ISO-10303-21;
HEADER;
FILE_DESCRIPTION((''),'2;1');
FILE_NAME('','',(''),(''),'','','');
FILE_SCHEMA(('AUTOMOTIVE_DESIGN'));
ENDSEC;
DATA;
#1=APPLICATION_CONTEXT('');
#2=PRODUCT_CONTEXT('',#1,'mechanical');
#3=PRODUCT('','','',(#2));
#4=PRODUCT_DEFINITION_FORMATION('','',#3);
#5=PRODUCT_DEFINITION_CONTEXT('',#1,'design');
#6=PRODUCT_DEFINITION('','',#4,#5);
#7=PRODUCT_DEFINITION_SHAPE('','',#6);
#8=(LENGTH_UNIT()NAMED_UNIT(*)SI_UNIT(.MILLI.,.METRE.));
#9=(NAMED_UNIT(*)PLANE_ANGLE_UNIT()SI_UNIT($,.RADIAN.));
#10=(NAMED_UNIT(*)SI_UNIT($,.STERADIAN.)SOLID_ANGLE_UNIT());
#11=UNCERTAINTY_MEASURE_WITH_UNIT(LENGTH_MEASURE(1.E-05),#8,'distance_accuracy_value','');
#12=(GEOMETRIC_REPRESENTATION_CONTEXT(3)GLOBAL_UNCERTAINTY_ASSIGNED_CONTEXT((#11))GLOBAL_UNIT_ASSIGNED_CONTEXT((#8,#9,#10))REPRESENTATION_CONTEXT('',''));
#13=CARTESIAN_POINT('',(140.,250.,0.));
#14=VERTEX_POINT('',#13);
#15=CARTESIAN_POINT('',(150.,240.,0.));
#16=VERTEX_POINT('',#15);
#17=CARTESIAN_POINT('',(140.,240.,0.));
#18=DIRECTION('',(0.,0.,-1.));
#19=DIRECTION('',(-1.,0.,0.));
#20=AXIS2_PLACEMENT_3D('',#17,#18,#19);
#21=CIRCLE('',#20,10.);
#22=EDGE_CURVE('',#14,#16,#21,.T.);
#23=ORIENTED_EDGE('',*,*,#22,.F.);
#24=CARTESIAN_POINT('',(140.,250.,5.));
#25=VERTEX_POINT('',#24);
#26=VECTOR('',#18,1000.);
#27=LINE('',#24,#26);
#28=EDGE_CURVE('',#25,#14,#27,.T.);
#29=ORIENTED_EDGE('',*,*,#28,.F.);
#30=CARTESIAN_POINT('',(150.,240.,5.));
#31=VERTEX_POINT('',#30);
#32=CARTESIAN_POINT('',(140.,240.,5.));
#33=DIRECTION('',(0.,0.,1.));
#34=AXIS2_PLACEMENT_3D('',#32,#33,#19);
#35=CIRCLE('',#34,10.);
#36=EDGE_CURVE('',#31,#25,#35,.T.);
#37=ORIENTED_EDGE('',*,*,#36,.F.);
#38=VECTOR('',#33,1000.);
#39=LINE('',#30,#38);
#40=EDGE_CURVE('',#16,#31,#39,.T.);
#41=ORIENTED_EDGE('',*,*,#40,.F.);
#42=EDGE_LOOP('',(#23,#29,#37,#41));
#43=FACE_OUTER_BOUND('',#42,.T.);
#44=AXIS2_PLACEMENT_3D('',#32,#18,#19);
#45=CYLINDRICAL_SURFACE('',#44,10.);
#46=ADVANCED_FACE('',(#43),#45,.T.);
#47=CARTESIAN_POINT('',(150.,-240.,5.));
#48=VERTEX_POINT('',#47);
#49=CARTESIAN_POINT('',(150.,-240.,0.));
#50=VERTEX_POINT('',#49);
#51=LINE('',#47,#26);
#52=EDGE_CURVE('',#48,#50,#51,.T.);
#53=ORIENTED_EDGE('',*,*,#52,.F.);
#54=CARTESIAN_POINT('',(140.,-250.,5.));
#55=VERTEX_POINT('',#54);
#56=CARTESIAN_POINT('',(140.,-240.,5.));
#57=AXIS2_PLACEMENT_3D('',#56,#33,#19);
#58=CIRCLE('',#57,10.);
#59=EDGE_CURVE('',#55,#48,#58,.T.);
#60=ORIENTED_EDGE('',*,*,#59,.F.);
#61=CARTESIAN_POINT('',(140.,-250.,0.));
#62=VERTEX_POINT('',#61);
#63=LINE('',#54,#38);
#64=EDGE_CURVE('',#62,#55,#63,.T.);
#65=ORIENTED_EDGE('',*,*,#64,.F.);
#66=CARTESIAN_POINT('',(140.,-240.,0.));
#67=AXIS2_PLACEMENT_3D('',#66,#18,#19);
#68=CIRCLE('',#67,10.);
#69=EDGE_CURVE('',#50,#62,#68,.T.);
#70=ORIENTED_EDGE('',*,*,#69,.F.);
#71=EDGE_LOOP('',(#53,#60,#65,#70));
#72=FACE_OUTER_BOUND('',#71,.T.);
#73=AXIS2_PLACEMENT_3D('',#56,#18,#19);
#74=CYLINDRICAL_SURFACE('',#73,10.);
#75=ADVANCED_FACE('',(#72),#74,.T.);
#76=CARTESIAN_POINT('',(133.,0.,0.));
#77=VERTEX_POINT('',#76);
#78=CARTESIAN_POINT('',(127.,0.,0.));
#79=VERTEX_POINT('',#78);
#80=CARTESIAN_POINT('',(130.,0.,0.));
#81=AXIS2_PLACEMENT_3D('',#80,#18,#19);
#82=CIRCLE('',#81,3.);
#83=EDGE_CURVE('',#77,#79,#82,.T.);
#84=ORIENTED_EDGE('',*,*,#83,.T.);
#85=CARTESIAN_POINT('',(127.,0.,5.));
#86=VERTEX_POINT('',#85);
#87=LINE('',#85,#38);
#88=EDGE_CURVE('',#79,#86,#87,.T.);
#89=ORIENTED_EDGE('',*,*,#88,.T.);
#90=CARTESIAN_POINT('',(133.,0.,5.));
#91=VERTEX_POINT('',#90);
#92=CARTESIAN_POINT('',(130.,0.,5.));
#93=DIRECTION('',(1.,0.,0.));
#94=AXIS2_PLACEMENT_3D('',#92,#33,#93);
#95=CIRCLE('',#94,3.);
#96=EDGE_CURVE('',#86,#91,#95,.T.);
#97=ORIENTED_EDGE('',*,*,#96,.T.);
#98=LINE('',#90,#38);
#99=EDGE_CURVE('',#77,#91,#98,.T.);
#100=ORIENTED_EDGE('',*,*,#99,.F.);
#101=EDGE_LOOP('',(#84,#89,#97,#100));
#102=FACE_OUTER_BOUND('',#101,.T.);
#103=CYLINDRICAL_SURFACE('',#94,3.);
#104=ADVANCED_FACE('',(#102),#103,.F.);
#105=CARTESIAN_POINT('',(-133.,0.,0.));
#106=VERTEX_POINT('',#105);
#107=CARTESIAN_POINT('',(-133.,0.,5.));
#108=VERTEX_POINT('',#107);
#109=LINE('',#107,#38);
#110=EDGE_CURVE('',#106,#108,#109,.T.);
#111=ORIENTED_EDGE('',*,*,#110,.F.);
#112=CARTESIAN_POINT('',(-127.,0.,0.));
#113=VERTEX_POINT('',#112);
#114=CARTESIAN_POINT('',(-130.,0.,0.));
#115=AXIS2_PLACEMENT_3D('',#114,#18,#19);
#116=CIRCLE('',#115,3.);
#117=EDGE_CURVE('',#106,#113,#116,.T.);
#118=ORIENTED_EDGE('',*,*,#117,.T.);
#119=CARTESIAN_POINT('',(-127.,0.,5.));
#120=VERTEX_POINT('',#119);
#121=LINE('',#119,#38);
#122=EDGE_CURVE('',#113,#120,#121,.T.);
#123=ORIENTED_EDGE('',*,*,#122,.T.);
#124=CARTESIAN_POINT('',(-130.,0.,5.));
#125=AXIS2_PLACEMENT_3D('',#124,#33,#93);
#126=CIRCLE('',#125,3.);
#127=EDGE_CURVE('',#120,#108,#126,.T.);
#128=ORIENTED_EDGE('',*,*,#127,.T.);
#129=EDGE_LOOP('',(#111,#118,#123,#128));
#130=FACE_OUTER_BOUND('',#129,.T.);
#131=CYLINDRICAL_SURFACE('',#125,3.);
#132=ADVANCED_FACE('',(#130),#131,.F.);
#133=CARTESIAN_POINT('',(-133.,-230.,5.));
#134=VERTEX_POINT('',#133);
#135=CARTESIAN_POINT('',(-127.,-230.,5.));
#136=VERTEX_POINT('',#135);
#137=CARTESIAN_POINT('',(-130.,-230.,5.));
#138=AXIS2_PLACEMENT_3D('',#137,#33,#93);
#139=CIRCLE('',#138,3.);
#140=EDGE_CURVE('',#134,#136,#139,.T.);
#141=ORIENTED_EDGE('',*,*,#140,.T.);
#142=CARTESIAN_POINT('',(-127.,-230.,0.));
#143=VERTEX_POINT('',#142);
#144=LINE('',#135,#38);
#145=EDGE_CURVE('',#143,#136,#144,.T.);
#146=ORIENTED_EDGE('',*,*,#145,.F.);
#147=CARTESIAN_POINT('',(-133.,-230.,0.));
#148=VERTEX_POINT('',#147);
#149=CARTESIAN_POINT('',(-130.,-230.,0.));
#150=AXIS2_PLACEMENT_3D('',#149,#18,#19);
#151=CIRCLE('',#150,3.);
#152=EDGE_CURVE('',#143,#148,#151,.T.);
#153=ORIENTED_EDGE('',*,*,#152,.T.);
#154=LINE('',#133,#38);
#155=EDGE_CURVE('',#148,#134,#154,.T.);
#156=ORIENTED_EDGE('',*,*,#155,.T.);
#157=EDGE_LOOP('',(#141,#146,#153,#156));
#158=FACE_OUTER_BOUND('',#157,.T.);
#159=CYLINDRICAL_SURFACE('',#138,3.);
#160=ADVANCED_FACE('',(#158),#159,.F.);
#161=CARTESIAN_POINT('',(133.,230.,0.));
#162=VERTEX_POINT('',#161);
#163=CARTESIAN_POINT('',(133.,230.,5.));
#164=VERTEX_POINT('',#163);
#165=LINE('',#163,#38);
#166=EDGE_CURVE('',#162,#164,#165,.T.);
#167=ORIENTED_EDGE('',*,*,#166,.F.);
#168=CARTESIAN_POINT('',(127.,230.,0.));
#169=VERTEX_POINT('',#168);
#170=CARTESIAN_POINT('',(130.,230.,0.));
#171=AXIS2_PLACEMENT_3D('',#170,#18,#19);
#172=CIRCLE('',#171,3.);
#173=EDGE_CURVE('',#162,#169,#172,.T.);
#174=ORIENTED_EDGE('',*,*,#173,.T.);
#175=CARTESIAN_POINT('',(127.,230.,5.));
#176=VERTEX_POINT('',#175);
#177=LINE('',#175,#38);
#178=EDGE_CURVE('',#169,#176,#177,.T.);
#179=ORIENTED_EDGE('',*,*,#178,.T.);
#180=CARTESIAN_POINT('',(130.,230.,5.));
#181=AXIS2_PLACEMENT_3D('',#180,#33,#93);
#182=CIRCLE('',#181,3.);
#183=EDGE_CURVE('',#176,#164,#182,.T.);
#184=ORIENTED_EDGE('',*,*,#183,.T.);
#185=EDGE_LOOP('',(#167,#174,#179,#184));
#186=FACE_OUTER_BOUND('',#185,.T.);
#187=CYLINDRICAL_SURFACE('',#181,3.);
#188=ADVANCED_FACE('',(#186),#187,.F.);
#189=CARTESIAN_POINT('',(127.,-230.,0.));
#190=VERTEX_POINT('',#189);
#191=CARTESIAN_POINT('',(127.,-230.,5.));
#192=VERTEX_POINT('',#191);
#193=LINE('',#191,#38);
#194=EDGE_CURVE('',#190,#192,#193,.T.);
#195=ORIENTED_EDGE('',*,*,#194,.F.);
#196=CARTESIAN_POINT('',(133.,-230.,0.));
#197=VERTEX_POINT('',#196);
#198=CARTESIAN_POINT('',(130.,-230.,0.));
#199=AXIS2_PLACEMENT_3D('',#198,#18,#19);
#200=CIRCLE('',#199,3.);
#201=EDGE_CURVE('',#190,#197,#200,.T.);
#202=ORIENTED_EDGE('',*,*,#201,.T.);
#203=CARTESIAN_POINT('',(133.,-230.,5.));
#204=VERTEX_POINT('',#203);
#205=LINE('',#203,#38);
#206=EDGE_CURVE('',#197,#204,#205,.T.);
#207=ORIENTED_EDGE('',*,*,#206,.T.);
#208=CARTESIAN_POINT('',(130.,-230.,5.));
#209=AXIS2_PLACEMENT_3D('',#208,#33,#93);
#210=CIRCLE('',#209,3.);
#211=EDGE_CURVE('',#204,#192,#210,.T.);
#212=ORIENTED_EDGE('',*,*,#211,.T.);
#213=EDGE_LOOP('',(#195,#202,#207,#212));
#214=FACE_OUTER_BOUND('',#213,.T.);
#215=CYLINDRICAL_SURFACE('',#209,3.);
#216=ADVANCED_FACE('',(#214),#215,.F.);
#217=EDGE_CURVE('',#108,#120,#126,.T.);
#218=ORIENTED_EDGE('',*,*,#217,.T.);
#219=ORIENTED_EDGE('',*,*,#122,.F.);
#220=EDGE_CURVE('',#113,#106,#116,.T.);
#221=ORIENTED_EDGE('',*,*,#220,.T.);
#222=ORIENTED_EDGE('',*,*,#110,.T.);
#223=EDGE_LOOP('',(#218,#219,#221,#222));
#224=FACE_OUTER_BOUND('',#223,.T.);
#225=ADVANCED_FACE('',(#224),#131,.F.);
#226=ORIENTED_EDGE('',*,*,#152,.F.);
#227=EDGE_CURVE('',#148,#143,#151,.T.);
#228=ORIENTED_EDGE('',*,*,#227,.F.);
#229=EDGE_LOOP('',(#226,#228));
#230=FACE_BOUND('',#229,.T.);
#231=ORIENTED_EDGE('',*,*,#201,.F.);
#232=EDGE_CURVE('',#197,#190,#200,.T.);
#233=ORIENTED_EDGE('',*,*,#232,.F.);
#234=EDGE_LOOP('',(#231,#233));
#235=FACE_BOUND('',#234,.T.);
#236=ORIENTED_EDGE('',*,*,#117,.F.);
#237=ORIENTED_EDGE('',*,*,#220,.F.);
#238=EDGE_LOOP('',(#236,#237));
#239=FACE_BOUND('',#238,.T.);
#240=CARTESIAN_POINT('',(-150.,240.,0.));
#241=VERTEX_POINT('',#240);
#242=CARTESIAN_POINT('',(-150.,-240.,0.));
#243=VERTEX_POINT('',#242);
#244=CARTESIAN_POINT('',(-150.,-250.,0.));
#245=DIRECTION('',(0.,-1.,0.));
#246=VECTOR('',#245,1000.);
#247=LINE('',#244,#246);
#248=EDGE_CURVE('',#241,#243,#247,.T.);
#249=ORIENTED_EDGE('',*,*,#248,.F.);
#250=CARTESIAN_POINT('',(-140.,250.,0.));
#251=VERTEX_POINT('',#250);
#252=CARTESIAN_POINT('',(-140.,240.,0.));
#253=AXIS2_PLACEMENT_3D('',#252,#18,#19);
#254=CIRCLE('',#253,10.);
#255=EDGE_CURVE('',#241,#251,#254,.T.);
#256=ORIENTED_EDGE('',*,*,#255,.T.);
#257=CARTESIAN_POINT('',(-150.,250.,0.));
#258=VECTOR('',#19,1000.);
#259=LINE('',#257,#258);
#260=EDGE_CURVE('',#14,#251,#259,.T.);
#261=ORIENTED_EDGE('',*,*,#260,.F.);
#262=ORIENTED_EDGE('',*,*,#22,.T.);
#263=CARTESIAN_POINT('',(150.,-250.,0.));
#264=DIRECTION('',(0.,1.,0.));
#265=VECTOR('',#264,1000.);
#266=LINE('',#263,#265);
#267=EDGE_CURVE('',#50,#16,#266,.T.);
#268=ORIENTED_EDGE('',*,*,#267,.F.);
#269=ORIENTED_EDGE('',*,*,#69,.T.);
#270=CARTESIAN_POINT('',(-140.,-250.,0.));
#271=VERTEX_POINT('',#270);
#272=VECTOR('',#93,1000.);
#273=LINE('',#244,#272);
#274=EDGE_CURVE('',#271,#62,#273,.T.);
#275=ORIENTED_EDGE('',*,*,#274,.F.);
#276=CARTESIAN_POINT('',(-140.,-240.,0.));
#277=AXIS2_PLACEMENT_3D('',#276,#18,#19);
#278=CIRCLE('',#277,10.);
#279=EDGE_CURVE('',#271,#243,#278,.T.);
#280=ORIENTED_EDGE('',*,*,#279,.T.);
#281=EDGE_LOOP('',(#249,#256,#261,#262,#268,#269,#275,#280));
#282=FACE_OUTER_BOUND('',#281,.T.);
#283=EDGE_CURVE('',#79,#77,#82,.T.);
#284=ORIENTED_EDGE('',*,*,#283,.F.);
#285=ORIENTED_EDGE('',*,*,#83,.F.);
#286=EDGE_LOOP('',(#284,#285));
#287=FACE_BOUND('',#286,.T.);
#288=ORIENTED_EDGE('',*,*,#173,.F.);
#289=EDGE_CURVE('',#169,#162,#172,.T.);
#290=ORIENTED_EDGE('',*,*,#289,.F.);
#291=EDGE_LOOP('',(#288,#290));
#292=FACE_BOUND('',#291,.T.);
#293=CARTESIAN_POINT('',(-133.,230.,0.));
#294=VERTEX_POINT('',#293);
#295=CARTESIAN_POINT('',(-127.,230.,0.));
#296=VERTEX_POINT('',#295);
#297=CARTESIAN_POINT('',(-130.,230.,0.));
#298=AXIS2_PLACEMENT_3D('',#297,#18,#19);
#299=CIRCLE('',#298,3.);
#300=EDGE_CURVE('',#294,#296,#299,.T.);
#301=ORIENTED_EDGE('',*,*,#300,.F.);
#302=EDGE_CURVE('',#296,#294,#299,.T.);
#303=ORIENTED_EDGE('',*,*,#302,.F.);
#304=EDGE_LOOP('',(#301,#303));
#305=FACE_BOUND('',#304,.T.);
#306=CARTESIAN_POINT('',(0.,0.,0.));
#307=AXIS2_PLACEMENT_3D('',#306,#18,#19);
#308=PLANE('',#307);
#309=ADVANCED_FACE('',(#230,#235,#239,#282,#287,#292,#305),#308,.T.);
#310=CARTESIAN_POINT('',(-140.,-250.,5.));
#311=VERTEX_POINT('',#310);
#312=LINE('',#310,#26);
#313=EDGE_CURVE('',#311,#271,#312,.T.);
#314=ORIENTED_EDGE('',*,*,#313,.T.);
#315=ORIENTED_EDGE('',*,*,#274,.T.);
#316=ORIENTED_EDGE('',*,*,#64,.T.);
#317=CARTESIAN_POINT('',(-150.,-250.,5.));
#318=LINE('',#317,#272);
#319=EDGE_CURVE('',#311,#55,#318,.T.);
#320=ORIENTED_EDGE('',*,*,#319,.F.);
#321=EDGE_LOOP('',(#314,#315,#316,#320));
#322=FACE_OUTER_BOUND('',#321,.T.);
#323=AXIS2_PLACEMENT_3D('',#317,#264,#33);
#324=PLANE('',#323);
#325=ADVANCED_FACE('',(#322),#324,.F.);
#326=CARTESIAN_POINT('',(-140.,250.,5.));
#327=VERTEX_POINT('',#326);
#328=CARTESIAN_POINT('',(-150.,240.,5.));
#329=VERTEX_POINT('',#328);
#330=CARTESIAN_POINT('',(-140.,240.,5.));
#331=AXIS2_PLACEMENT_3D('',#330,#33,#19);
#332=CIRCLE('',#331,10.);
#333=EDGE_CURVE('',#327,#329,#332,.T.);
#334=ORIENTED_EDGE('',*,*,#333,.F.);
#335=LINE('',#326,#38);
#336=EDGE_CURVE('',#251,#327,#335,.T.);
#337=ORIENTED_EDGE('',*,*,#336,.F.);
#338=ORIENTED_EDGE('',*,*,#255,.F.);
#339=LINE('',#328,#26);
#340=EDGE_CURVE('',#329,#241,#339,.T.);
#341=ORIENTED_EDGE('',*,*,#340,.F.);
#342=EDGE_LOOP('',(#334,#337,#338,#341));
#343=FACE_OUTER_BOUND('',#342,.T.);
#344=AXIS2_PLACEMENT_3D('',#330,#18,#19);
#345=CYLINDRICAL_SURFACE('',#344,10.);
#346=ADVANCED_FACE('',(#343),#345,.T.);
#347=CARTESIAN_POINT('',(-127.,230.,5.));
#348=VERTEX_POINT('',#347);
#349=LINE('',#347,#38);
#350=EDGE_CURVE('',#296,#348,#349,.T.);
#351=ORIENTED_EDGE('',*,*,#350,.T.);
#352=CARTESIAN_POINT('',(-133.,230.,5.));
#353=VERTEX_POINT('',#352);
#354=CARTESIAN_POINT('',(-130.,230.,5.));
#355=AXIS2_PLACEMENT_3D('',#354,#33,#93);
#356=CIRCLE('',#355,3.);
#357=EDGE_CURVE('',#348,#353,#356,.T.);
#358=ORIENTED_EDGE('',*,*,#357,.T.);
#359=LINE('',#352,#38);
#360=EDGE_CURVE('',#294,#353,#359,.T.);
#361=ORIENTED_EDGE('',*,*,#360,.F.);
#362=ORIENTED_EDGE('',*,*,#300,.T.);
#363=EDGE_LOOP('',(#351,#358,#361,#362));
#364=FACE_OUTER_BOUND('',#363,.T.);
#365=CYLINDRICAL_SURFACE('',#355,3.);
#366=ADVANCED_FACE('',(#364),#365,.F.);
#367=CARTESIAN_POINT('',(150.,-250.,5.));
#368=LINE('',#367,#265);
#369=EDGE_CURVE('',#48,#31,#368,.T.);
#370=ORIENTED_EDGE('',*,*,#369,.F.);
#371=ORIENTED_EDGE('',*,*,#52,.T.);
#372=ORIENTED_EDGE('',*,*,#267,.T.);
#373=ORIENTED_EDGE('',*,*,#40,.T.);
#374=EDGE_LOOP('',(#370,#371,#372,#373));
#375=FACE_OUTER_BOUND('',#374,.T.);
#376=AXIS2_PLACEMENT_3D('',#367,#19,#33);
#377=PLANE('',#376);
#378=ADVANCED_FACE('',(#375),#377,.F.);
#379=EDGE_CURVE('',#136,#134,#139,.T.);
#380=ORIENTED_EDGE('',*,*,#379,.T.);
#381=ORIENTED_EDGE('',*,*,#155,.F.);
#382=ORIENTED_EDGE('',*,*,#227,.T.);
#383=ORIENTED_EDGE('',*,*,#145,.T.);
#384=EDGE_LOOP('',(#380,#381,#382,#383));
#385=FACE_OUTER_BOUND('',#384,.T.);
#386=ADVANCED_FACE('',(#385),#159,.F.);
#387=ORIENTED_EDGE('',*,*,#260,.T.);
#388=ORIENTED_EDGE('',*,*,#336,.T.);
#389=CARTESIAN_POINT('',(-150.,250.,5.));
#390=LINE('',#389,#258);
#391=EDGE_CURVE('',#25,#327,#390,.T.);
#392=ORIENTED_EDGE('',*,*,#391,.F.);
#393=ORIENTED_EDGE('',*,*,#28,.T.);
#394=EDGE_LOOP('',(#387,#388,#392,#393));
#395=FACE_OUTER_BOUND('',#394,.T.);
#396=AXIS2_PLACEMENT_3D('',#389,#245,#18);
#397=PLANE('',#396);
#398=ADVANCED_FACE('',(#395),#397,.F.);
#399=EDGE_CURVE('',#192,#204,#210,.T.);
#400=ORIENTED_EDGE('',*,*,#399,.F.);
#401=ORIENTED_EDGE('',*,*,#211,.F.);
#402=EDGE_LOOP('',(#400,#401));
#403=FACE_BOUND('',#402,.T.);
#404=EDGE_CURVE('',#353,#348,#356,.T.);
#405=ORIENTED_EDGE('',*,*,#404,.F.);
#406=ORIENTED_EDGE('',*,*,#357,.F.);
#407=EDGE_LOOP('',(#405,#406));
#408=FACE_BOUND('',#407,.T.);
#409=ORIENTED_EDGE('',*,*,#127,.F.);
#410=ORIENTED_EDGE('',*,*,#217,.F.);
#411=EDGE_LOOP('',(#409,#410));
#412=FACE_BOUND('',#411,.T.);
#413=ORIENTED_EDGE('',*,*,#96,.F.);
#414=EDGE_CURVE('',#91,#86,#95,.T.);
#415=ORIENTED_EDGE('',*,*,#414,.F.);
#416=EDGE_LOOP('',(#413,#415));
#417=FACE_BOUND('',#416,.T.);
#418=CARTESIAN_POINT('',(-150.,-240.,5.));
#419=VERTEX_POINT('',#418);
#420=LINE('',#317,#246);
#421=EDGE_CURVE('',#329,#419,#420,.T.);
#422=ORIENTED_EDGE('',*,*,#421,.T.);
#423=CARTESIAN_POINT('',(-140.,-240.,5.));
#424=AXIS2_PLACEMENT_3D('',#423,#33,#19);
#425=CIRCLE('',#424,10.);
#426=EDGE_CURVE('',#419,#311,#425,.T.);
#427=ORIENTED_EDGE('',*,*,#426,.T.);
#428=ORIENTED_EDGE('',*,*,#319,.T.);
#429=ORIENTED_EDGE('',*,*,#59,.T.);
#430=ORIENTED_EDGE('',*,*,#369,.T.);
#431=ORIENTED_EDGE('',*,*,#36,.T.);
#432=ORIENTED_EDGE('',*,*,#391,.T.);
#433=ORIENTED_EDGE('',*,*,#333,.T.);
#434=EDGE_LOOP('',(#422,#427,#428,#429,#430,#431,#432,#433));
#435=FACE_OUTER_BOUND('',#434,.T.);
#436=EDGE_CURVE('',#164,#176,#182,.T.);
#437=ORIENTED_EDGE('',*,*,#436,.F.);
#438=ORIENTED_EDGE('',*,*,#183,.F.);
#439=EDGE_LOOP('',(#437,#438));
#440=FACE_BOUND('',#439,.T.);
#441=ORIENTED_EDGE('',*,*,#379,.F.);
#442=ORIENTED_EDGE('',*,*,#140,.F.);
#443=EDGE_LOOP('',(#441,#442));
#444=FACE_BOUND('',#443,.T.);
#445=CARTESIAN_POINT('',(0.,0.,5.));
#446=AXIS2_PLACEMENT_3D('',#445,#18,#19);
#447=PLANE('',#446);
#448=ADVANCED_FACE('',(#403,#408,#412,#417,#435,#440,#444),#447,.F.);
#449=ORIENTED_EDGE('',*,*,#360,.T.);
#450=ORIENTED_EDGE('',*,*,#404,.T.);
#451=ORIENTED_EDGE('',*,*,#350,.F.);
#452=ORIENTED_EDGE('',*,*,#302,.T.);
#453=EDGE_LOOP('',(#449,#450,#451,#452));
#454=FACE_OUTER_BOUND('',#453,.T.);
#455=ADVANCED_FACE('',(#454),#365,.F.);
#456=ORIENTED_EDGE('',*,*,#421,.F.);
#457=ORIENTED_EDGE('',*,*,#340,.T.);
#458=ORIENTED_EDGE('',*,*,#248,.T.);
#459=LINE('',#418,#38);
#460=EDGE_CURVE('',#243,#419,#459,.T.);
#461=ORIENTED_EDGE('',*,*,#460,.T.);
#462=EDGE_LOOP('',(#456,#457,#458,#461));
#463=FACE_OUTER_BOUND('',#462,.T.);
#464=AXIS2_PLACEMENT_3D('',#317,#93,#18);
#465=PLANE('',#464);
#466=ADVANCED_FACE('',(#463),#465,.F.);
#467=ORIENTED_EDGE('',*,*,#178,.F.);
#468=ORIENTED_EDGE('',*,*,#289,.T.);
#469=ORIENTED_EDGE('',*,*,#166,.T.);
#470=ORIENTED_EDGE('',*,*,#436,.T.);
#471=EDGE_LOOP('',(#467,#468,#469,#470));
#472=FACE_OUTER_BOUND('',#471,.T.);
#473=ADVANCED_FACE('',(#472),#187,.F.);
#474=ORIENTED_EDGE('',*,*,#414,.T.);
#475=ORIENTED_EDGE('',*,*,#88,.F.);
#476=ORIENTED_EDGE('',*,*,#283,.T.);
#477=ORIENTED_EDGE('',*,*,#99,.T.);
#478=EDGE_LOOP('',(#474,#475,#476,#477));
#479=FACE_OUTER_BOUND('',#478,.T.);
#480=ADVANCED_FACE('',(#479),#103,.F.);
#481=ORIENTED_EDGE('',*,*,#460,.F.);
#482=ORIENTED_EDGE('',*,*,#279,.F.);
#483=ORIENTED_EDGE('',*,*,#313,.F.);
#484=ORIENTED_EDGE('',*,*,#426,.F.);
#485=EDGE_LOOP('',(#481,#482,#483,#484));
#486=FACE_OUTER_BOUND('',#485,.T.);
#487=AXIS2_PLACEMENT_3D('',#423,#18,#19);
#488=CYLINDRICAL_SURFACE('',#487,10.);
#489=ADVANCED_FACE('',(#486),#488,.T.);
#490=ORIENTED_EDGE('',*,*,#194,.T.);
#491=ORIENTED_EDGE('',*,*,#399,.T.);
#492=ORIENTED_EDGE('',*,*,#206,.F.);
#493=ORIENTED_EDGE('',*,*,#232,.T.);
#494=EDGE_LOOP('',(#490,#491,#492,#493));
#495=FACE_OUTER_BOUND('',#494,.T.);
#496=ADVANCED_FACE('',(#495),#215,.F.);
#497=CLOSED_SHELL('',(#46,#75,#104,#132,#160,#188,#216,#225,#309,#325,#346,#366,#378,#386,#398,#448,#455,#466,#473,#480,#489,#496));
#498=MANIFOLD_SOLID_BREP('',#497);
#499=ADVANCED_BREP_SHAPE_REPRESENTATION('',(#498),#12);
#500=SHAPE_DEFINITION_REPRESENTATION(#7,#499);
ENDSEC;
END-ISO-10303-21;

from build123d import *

# Parameters (mm, degrees)
SKETCH_1_W                = 300
SKETCH_1_H                = 500
EXTRUDE_1_DEPTH           = 5
HOLE_WIZARD_6_0_6_1_D     = 6
HOLE_WIZARD_6_0_6_1_DEPTH = 27.75
HOLE_WIZARD_6_0_6_1_TIP   = 1.802581857
FILLET_1_R                = 10


with BuildPart() as part:
    # 草图1 → 凸台-拉伸1 (new body)
    with BuildSketch(Plane.XY):
        Rectangle(SKETCH_1_W, SKETCH_1_H)
    extrude(amount=EXTRUDE_1_DEPTH)

    # Ø6.0 (6) 直径孔1
    with Locations(Plane.XY.offset(5)):
        with Locations((-130, 230), (130, 230), (130, -230), (-130, -230), (-130, 0), (130, 0)):
            Hole(HOLE_WIZARD_6_0_6_1_D / 2, depth=HOLE_WIZARD_6_0_6_1_DEPTH)
            with Locations((0, 0, -(HOLE_WIZARD_6_0_6_1_DEPTH + HOLE_WIZARD_6_0_6_1_TIP / 2))):  # 118° drill point
                Cone(0, HOLE_WIZARD_6_0_6_1_D / 2, HOLE_WIZARD_6_0_6_1_TIP, mode=Mode.SUBTRACT)

    # 圆角1
    fillet_1_edges = [part.edges().sort_by_distance(p)[0] for p in [
        (150, -250, 2.5),
        (-150, -250, 2.5),
        (-150, 250, 2.5),
        (150, 250, 2.5),
    ]]
    fillet(fillet_1_edges, radius=FILLET_1_R)


solid = part.part
